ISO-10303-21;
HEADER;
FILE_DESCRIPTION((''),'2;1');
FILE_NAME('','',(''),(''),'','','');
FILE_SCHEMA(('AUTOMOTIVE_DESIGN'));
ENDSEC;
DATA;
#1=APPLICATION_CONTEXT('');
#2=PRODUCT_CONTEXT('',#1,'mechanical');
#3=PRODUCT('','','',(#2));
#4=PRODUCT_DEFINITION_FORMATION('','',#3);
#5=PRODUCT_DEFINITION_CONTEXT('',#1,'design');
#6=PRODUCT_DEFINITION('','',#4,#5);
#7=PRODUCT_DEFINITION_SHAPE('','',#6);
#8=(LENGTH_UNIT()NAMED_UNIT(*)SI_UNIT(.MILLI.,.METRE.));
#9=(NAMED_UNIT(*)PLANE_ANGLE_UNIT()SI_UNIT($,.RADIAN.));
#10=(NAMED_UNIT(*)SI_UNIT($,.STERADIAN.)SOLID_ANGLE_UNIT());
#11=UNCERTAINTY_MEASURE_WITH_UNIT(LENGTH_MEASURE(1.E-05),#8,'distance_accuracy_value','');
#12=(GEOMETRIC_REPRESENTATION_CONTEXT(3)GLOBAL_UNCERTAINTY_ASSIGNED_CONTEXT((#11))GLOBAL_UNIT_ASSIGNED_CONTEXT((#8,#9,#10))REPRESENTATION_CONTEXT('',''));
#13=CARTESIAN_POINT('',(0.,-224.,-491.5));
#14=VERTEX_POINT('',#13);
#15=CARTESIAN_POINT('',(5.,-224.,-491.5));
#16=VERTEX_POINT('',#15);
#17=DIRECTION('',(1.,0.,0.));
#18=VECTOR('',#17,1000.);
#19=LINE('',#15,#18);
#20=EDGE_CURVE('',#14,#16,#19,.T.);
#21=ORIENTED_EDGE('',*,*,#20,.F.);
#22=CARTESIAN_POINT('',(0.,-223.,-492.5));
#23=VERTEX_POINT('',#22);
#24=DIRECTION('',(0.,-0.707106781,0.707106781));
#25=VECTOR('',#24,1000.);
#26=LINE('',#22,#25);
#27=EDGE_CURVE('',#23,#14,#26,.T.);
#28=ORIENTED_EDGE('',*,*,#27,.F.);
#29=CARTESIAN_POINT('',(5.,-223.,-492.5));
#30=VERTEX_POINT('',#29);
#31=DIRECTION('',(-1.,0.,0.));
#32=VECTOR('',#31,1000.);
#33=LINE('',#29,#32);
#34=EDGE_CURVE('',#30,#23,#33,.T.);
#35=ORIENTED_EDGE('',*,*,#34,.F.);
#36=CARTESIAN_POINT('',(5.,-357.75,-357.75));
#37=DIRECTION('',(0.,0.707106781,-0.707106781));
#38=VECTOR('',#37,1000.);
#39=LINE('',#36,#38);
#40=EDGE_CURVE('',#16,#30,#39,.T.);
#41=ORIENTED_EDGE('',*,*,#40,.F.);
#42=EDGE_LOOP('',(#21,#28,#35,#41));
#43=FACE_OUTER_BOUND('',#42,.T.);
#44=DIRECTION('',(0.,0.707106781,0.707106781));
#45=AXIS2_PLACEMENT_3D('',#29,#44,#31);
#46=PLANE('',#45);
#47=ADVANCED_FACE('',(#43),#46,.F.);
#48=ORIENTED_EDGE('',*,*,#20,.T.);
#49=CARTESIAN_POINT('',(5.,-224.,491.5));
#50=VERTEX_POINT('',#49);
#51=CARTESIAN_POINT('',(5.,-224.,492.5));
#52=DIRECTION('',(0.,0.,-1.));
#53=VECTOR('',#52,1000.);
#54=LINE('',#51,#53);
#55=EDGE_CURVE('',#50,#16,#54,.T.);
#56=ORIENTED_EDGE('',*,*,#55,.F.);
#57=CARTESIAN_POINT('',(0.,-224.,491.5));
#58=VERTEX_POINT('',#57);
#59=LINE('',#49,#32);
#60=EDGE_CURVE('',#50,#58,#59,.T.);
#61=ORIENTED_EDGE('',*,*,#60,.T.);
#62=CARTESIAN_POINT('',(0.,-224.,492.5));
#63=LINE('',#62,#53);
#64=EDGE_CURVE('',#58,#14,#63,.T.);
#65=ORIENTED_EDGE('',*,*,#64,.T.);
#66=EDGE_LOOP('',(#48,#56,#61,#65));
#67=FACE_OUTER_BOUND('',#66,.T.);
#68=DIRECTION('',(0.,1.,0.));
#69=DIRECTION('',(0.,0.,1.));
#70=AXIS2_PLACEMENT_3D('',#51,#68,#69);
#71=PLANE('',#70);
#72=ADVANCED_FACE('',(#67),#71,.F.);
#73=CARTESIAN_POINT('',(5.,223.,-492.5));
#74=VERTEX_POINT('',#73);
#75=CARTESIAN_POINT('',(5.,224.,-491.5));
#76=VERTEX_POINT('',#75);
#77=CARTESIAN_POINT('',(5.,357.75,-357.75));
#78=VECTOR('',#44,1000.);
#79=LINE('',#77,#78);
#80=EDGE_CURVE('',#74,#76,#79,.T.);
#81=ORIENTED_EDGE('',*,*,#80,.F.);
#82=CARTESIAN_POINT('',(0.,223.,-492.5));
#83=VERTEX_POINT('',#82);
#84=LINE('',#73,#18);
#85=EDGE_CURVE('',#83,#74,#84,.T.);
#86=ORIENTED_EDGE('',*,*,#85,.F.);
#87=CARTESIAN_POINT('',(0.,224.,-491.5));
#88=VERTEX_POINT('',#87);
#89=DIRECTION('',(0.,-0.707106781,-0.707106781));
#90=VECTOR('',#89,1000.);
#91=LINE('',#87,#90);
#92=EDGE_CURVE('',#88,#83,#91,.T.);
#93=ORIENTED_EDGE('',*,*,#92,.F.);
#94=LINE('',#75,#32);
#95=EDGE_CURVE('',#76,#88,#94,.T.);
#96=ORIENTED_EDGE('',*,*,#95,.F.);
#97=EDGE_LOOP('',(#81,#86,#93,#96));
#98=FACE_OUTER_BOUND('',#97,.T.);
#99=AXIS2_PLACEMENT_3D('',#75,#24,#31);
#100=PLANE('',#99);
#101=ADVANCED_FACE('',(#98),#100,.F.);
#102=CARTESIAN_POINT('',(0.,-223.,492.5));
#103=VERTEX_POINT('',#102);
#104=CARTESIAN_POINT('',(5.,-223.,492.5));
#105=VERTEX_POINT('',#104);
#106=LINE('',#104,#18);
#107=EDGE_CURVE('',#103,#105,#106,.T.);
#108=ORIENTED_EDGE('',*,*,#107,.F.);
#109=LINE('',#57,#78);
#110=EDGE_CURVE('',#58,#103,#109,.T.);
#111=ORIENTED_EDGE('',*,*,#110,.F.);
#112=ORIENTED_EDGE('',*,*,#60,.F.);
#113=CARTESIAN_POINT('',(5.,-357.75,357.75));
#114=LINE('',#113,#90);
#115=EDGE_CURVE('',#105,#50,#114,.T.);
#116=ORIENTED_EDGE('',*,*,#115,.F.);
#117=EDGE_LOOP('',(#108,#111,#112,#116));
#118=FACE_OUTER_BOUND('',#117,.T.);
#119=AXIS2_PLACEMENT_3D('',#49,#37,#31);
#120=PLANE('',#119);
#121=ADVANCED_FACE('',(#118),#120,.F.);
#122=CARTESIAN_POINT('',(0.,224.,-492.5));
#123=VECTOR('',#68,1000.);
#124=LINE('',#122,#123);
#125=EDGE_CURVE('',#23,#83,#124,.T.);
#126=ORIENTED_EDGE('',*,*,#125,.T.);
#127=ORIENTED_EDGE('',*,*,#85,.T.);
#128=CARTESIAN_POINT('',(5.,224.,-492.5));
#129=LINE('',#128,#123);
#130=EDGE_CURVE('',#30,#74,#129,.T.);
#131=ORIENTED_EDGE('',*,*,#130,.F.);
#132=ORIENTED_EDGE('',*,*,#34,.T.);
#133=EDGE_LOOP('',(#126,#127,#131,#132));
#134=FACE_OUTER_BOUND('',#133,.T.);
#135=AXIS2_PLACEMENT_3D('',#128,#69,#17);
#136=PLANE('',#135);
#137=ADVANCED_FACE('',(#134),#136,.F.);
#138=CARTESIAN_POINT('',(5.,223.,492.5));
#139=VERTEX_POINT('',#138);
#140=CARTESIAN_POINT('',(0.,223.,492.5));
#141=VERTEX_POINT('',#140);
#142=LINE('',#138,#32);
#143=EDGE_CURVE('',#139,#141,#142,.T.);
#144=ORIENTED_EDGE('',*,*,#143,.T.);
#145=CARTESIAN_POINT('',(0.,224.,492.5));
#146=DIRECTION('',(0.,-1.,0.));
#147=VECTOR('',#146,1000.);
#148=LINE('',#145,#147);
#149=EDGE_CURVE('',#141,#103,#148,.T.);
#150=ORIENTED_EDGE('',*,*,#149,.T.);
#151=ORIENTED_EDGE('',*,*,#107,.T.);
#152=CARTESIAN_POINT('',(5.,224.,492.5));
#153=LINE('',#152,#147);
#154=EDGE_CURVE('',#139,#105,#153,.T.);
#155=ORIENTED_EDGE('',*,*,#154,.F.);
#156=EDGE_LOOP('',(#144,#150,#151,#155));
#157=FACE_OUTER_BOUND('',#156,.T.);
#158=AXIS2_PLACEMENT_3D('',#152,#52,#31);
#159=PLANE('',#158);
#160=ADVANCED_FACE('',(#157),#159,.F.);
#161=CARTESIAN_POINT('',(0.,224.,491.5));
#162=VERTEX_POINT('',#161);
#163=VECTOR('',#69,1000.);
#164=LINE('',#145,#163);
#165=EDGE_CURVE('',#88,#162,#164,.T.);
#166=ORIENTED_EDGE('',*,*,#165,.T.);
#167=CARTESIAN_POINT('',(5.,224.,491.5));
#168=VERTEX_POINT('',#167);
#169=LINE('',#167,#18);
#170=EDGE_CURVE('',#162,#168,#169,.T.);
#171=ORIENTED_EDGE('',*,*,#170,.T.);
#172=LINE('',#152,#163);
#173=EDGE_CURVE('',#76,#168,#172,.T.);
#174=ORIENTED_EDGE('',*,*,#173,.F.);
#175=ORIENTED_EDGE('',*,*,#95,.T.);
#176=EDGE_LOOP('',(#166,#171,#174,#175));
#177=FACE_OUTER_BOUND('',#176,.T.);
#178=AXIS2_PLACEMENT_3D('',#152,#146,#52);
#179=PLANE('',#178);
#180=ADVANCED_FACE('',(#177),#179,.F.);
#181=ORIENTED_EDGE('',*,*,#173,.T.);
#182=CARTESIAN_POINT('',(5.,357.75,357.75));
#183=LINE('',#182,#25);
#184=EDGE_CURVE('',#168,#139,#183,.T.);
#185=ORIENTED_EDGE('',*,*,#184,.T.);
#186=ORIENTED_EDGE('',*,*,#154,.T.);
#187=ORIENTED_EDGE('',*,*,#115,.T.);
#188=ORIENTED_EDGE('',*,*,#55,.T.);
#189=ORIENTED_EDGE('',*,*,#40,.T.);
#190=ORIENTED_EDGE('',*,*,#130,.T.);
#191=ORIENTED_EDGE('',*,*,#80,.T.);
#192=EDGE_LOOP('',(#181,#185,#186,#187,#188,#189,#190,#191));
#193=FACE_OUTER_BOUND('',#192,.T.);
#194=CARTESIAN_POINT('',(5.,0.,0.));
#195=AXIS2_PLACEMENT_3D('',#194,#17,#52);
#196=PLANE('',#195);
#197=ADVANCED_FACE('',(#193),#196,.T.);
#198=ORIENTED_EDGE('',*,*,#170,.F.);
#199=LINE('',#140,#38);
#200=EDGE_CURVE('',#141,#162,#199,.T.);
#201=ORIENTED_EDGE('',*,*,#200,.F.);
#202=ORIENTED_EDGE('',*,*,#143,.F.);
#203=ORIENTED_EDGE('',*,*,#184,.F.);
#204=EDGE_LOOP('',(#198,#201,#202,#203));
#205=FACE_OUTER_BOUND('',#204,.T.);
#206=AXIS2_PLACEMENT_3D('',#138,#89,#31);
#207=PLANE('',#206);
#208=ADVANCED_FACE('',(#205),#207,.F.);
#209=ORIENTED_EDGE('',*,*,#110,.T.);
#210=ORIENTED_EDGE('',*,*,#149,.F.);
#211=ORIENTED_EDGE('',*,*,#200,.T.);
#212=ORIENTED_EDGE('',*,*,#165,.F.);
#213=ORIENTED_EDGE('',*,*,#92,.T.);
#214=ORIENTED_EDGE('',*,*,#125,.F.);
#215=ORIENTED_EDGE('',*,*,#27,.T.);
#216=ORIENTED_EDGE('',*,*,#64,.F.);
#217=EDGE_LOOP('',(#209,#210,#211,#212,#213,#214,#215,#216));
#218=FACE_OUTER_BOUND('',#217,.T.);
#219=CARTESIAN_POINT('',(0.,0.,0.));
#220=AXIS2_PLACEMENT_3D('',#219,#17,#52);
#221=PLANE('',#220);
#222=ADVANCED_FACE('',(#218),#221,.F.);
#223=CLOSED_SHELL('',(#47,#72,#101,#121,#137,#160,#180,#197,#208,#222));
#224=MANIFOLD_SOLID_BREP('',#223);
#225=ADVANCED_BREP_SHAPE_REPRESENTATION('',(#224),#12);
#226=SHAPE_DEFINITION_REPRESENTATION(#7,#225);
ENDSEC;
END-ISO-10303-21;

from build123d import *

# Parameters (mm, degrees)
SKETCH_2_W      = 985
SKETCH_2_H      = 448
EXTRUDE_1_DEPTH = 5
CHAMFER_1_SIZE  = 1


with BuildPart() as part:
    # 草图2 → 凸台-拉伸1 (new body)
    with BuildSketch(Plane(origin=(0, 0, 0), x_dir=(0, 0, -1), z_dir=(1, 0, 0))):
        Rectangle(SKETCH_2_W, SKETCH_2_H)
    extrude(amount=EXTRUDE_1_DEPTH)

    # 倒角1
    chamfer_1_edges = [part.edges().sort_by_distance(p)[0] for p in [
        (2.5, -224, -492.5),
        (2.5, -224, 492.5),
        (2.5, 224, 492.5),
        (2.5, 224, -492.5),
    ]]
    chamfer(chamfer_1_edges, length=CHAMFER_1_SIZE)


solid = part.part
